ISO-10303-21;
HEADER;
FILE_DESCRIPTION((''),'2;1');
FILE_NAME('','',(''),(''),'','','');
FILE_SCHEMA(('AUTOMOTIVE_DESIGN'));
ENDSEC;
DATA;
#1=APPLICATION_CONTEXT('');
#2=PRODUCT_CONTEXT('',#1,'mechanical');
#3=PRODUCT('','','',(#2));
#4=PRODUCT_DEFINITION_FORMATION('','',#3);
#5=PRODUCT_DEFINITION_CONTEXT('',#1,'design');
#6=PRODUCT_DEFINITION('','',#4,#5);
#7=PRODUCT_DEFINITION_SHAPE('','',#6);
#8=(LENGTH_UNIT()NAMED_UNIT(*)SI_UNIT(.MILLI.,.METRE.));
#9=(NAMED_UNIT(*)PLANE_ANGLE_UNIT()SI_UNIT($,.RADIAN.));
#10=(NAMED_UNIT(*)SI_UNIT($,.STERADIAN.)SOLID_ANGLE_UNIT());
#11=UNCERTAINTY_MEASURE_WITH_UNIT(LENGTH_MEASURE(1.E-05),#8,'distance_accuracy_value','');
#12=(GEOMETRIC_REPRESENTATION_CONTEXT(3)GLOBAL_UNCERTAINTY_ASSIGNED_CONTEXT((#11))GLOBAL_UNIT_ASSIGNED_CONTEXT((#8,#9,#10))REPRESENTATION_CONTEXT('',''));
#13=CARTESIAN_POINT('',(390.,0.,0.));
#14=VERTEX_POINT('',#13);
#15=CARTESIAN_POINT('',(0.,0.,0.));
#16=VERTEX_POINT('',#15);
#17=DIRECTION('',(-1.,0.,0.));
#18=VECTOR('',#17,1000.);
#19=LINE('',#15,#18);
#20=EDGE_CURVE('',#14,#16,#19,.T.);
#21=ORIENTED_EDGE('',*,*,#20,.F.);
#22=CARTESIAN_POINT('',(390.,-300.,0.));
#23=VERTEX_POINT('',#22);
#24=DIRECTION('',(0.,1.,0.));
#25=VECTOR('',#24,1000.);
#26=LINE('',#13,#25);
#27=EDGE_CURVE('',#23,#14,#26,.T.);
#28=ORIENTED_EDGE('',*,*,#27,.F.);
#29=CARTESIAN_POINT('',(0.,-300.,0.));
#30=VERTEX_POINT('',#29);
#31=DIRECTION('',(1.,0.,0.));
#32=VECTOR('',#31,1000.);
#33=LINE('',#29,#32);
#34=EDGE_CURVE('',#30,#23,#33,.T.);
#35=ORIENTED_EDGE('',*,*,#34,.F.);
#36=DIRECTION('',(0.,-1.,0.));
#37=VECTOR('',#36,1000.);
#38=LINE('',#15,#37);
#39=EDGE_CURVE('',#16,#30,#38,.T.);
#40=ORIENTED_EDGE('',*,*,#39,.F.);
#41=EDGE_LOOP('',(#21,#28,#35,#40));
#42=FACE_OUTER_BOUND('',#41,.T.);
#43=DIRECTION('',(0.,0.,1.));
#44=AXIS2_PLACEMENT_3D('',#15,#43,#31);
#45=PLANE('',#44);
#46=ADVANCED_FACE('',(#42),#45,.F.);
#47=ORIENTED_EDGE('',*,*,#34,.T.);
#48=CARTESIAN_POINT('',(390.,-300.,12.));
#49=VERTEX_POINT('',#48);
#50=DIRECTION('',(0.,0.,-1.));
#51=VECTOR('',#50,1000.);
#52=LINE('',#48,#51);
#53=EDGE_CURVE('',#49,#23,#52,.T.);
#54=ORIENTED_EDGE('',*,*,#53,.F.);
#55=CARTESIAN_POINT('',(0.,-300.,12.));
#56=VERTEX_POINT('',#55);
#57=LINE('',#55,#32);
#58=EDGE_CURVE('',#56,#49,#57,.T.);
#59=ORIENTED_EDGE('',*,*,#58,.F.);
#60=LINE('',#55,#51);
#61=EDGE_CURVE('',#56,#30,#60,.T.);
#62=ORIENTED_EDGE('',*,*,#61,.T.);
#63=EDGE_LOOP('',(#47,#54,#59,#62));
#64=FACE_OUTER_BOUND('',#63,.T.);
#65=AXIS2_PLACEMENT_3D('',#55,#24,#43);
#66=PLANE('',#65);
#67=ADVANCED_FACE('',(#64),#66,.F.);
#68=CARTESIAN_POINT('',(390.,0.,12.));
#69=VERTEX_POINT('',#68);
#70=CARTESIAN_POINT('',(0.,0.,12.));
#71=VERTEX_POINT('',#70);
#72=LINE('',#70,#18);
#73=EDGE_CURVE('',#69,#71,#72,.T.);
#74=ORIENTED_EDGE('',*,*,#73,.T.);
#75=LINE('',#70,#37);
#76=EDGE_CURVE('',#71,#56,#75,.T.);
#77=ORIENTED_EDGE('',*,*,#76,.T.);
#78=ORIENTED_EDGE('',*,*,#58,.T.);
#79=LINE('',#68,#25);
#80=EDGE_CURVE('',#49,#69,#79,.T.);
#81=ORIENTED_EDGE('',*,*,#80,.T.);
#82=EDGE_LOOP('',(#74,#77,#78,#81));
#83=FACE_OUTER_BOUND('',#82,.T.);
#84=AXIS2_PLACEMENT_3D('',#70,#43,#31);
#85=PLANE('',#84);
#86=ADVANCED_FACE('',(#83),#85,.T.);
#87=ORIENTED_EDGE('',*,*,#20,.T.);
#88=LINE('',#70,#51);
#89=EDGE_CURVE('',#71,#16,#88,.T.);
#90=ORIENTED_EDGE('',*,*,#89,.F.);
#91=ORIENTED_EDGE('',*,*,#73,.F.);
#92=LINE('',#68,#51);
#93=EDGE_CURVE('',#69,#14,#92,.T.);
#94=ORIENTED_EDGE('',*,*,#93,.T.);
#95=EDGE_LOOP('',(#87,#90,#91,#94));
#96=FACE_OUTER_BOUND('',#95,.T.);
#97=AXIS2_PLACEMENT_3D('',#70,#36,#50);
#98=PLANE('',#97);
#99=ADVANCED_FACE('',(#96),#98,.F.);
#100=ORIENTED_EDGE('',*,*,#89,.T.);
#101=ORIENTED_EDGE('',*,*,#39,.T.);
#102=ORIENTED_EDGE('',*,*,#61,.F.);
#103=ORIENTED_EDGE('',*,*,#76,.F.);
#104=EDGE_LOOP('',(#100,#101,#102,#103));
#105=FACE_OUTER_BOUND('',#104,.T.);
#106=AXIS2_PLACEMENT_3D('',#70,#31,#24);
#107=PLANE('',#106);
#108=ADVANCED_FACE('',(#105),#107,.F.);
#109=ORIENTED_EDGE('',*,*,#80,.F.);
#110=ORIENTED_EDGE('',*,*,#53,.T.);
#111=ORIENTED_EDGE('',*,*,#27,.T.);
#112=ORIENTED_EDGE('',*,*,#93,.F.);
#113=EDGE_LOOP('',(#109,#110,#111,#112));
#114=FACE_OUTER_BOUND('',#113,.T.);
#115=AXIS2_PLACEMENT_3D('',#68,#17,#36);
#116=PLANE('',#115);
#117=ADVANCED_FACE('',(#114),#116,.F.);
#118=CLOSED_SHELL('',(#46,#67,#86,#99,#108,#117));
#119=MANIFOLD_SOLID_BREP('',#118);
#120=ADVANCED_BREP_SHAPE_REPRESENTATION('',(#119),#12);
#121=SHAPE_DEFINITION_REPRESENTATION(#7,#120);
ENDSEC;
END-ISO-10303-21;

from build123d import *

# Parameters (mm, degrees)
SKETCH1_W           = 390
SKETCH1_H           = 300
BOSS_EXTRUDE1_DEPTH = 12


with BuildPart() as part:
    # Sketch1 → Boss-Extrude1 (new body)
    with BuildSketch(Plane.XY):
        with Locations((195, -150)):
            Rectangle(SKETCH1_W, SKETCH1_H)
    extrude(amount=BOSS_EXTRUDE1_DEPTH)


solid = part.part
